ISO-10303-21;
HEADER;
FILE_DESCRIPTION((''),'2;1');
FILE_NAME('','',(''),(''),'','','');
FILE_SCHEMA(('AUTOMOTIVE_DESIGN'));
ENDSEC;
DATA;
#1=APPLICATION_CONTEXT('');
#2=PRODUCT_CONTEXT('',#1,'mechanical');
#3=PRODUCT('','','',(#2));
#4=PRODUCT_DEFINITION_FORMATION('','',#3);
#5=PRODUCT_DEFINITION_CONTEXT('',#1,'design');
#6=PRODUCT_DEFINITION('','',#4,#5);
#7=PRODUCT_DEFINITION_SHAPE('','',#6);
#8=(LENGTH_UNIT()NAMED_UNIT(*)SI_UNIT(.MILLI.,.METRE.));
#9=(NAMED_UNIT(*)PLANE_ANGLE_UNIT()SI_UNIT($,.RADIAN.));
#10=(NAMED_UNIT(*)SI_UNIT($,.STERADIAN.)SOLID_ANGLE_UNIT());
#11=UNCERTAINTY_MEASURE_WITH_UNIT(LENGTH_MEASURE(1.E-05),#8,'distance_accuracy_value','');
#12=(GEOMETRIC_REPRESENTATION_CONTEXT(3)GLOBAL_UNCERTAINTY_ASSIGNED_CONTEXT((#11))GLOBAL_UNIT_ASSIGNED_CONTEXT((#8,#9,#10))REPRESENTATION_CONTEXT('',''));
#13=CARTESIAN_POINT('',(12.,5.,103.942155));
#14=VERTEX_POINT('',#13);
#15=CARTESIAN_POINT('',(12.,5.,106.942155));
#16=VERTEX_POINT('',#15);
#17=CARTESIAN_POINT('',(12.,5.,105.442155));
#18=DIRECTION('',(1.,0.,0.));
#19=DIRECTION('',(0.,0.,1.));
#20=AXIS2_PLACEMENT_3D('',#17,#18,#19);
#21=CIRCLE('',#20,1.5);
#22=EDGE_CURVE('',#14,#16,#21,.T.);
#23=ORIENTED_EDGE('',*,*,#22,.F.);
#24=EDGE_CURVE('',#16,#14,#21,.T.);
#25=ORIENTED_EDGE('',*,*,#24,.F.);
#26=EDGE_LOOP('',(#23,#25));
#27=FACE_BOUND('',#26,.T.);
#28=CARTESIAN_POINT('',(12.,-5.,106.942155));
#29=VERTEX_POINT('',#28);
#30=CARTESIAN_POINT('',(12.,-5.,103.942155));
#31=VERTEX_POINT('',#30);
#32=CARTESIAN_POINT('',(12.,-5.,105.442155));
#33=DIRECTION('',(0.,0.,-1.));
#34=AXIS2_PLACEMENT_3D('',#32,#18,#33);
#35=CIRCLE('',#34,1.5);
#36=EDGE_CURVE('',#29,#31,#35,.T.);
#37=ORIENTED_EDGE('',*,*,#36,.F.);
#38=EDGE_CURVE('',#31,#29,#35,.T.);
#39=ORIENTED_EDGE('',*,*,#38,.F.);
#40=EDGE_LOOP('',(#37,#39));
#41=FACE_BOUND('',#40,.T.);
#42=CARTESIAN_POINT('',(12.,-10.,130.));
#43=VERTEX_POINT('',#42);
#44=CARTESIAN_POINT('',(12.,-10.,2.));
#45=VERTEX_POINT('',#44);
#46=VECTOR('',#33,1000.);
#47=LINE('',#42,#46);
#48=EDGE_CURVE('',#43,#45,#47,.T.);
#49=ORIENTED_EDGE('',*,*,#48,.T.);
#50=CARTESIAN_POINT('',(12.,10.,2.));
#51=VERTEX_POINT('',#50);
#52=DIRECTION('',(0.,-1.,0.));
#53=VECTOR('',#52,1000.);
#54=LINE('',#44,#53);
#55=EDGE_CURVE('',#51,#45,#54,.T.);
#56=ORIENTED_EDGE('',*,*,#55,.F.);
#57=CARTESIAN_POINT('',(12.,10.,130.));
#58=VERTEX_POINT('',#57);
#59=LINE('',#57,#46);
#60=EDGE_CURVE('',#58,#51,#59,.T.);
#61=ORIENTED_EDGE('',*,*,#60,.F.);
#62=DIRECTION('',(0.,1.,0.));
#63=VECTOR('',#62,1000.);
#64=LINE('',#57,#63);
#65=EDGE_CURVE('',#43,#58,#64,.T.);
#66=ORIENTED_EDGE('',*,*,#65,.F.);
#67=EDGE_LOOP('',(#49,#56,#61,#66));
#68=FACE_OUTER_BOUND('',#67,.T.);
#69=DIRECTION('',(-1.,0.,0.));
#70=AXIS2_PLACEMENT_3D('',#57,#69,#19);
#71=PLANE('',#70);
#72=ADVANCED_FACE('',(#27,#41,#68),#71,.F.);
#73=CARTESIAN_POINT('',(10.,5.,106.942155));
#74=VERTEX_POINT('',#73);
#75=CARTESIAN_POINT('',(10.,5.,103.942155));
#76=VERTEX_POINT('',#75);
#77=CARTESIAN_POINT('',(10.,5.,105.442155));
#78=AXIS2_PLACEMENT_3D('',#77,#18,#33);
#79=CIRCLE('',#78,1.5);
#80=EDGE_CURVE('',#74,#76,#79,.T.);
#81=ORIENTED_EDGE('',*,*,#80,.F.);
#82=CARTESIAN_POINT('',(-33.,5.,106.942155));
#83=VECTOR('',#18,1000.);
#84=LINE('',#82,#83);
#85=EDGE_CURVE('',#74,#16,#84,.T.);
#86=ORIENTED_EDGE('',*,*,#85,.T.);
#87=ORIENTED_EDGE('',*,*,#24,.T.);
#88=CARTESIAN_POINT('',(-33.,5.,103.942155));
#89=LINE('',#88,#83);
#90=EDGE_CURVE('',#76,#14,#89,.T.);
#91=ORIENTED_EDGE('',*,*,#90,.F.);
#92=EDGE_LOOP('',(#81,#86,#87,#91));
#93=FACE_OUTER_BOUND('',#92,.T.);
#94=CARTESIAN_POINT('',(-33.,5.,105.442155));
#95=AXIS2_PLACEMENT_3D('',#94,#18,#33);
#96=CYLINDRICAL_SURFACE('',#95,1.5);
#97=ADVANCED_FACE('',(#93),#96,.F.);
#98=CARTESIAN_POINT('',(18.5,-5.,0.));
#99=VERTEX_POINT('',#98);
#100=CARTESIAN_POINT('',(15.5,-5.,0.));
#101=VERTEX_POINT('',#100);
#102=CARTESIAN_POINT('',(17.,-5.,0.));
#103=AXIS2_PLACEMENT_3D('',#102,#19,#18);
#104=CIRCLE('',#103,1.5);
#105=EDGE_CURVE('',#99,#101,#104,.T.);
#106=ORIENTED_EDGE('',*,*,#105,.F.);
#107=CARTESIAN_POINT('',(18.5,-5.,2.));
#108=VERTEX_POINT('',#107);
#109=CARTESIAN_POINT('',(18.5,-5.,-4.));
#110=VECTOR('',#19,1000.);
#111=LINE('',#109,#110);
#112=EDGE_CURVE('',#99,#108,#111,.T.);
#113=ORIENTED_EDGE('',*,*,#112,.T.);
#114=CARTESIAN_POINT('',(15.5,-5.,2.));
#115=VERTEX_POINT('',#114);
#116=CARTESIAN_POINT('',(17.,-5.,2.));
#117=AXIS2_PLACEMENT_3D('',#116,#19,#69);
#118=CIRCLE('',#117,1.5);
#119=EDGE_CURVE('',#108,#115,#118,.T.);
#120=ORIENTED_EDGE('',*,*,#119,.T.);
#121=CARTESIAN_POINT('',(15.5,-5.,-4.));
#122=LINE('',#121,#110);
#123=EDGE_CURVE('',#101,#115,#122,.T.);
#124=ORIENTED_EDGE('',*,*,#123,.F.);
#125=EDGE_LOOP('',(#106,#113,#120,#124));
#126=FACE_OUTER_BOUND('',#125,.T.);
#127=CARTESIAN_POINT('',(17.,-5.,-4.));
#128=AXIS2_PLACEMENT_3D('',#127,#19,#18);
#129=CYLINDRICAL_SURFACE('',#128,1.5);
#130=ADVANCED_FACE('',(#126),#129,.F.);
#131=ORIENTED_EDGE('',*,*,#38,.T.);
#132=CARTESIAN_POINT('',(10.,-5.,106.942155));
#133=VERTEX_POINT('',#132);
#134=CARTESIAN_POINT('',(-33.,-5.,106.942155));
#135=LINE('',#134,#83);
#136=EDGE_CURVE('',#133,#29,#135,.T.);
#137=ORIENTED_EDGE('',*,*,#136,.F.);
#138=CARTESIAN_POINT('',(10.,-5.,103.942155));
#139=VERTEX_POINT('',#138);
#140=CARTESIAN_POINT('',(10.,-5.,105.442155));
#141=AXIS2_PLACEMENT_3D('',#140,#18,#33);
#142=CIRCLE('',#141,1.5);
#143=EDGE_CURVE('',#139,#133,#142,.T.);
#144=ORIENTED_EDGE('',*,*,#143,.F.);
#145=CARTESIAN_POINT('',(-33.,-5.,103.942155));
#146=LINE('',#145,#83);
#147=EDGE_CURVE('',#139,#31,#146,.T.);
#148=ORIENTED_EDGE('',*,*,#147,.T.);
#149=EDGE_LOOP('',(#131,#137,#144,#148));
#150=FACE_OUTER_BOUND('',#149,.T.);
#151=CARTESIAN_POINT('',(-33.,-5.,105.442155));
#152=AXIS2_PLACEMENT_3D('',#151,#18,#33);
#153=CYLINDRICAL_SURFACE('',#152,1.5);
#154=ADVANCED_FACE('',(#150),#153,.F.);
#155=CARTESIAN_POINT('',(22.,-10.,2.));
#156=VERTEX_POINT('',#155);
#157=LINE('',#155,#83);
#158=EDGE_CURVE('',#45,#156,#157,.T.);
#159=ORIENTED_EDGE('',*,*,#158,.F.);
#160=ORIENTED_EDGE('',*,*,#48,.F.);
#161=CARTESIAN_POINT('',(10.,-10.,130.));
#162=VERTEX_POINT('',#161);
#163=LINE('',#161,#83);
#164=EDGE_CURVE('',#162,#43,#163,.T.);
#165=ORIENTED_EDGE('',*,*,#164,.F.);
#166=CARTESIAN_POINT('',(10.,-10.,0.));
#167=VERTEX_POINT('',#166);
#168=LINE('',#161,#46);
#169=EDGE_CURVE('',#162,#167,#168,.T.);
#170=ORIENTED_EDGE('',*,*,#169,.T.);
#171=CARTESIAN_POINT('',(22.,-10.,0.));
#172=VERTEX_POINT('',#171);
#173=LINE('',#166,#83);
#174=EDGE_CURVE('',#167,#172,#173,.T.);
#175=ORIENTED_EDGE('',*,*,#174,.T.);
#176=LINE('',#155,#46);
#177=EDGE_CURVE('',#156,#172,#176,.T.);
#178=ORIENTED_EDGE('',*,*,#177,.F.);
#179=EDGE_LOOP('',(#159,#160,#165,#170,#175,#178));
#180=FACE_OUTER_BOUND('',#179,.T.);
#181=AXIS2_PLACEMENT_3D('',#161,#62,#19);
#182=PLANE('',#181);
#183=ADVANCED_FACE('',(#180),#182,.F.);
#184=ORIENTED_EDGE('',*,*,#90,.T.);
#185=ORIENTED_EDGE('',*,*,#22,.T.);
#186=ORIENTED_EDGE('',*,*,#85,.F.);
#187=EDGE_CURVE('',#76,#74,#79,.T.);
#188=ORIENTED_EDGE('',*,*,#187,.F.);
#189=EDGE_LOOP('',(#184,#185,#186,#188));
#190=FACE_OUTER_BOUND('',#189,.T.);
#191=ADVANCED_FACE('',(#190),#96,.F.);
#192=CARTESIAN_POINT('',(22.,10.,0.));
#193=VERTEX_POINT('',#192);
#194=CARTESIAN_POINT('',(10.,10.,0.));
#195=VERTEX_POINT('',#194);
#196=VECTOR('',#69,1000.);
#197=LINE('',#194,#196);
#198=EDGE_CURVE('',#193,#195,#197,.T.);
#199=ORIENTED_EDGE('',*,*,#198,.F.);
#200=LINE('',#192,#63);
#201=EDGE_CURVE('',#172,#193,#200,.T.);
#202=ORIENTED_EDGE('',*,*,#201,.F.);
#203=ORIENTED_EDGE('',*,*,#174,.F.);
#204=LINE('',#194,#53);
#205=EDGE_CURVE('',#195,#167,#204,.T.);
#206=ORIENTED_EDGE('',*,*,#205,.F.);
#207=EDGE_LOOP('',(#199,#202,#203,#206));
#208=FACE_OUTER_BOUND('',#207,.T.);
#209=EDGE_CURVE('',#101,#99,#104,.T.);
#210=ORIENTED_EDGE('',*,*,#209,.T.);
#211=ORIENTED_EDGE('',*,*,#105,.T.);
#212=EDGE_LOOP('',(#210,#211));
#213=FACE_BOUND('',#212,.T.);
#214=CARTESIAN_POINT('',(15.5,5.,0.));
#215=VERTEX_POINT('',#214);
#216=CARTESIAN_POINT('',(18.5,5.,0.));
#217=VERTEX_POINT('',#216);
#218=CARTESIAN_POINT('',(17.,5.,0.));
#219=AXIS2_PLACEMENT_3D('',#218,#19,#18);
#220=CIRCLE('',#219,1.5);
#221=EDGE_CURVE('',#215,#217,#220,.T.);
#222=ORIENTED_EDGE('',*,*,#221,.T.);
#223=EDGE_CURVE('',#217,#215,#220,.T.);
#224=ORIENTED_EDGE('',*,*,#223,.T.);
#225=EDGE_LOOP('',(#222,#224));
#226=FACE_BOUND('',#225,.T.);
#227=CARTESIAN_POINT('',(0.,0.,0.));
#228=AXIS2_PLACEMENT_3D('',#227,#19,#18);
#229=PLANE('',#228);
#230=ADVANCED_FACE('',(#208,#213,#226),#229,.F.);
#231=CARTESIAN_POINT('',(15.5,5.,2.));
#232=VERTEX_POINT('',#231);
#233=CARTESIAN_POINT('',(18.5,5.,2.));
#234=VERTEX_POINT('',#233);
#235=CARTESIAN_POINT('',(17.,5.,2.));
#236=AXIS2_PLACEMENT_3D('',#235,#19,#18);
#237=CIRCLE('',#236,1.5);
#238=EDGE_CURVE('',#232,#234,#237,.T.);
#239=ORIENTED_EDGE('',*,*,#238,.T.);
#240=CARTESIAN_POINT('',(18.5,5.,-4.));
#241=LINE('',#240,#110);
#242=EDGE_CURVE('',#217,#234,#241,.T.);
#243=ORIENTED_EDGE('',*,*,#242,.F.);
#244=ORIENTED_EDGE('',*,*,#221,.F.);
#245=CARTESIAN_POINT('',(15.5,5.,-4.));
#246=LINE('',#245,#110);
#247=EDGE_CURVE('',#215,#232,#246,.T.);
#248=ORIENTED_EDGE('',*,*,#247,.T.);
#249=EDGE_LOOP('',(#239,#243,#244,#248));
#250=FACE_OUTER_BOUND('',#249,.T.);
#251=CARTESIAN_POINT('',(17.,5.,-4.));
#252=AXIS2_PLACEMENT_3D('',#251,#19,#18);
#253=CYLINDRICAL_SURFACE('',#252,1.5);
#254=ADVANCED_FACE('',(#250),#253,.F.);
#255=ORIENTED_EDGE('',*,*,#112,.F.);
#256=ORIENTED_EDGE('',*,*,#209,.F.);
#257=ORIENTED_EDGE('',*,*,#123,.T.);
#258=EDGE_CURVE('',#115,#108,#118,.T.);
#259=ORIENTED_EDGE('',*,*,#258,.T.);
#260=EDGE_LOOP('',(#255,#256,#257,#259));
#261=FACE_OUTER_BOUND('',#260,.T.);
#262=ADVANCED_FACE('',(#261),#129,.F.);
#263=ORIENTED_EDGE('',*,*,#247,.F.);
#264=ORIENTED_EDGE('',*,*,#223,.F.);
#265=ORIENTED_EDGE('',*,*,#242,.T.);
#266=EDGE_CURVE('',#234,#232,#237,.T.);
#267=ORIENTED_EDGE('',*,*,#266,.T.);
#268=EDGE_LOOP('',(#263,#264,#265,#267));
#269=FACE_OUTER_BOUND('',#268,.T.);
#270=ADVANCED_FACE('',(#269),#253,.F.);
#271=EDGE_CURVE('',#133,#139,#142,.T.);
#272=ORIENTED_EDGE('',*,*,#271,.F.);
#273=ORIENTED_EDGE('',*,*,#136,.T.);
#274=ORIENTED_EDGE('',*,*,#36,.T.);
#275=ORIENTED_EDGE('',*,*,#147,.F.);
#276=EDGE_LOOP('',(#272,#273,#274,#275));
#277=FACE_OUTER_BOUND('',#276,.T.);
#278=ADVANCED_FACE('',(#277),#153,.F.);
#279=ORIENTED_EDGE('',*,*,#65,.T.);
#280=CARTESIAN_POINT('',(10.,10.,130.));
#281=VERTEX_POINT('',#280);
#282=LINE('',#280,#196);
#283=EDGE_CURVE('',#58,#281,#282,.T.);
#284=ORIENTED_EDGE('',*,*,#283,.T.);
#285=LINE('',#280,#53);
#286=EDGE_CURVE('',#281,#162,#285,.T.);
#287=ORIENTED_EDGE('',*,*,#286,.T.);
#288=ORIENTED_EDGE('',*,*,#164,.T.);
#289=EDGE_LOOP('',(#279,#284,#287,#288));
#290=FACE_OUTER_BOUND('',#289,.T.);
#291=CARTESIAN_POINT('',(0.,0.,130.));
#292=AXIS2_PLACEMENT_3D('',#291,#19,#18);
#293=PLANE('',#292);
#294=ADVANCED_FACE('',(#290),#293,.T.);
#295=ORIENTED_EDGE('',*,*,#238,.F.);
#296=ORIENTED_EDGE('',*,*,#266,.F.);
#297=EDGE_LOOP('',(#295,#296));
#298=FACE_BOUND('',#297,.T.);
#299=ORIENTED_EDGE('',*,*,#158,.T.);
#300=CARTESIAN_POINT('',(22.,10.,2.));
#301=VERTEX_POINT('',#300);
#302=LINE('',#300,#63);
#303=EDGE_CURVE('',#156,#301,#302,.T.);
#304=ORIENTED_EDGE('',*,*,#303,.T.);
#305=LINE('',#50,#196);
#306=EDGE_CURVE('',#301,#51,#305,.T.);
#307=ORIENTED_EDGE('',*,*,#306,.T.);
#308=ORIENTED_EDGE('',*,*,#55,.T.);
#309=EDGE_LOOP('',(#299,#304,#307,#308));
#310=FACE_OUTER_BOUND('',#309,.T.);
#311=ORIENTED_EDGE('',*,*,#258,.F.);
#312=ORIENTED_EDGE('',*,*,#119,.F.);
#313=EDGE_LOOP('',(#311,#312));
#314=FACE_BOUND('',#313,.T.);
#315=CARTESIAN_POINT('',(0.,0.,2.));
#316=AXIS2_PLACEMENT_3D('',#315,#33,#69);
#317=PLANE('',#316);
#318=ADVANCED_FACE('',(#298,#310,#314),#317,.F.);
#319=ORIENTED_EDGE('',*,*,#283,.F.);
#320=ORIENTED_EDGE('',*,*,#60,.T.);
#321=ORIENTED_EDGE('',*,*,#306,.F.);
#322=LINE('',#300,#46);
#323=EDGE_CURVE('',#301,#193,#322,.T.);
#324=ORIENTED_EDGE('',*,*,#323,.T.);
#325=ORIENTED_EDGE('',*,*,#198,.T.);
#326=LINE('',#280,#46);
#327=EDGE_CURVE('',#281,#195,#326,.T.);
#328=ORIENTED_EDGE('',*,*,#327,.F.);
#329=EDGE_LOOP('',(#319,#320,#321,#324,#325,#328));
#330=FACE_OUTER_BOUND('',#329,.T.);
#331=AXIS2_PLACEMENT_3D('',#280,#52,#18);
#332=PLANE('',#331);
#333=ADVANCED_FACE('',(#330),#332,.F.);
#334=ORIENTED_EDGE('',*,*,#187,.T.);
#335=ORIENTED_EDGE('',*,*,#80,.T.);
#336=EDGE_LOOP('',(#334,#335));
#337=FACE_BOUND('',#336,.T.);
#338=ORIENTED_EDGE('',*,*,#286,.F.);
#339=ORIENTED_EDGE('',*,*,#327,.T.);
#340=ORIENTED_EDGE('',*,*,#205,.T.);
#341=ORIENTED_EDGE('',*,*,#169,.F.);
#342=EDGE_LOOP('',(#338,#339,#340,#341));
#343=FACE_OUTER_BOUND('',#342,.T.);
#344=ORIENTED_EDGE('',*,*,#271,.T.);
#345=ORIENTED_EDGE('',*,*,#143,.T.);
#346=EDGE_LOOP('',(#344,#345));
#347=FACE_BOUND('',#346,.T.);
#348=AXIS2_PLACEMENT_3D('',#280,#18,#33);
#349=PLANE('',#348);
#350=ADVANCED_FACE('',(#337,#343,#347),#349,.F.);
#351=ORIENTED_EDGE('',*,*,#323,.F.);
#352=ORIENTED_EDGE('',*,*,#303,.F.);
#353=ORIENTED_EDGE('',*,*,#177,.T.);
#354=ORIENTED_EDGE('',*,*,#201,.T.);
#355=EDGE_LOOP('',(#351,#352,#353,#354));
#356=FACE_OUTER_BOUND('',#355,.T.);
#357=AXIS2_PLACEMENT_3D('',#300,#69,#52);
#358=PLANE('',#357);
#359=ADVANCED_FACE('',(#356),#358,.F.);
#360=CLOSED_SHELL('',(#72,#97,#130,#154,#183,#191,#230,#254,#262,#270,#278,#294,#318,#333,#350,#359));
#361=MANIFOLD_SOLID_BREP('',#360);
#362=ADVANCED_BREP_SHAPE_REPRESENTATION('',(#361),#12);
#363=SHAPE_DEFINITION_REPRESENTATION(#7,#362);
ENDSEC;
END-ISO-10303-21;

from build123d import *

# Parameters (mm, degrees)
SKETCH1_W           = 2
SKETCH1_H           = 20
BOSS_EXTRUDE1_DEPTH = 130
SKETCH2_W           = 10
SKETCH2_H           = 20
BOSS_EXTRUDE2_DEPTH = 2
SKETCH3_R           = 1.5
CUT_EXTRUDE1_DEPTH  = 6
SKETCH5_R           = 1.5
CUT_EXTRUDE2_DEPTH  = 45


with BuildPart() as part:
    # Sketch1 → Boss-Extrude1 (new body)
    with BuildSketch(Plane.XY):
        with Locations((11, 0)):
            Rectangle(SKETCH1_W, SKETCH1_H)
    extrude(amount=BOSS_EXTRUDE1_DEPTH)

    # Sketch2 → Boss-Extrude2 (add)
    with BuildSketch(Plane.XY):
        with Locations((17, 0)):
            Rectangle(SKETCH2_W, SKETCH2_H)
    extrude(amount=BOSS_EXTRUDE2_DEPTH)

    # Sketch3 → Cut-Extrude1 (cut)
    with BuildSketch(Plane.XY.offset(2)):
        with Locations((17, 5)):
            Circle(SKETCH3_R)
        with Locations((17, -5)):
            Circle(SKETCH3_R)
    extrude(amount=-CUT_EXTRUDE1_DEPTH, mode=Mode.SUBTRACT)

    # Sketch5 → Cut-Extrude2 (cut)
    with BuildSketch(Plane(origin=(12, 0, 0), x_dir=(0, 0, -1), z_dir=(1, 0, 0))):
        with Locations((-105.442155364, -5)):
            Circle(SKETCH5_R)
        with Locations((-105.442155364, 5)):
            Circle(SKETCH5_R)
    extrude(amount=-CUT_EXTRUDE2_DEPTH, mode=Mode.SUBTRACT)


solid = part.part
